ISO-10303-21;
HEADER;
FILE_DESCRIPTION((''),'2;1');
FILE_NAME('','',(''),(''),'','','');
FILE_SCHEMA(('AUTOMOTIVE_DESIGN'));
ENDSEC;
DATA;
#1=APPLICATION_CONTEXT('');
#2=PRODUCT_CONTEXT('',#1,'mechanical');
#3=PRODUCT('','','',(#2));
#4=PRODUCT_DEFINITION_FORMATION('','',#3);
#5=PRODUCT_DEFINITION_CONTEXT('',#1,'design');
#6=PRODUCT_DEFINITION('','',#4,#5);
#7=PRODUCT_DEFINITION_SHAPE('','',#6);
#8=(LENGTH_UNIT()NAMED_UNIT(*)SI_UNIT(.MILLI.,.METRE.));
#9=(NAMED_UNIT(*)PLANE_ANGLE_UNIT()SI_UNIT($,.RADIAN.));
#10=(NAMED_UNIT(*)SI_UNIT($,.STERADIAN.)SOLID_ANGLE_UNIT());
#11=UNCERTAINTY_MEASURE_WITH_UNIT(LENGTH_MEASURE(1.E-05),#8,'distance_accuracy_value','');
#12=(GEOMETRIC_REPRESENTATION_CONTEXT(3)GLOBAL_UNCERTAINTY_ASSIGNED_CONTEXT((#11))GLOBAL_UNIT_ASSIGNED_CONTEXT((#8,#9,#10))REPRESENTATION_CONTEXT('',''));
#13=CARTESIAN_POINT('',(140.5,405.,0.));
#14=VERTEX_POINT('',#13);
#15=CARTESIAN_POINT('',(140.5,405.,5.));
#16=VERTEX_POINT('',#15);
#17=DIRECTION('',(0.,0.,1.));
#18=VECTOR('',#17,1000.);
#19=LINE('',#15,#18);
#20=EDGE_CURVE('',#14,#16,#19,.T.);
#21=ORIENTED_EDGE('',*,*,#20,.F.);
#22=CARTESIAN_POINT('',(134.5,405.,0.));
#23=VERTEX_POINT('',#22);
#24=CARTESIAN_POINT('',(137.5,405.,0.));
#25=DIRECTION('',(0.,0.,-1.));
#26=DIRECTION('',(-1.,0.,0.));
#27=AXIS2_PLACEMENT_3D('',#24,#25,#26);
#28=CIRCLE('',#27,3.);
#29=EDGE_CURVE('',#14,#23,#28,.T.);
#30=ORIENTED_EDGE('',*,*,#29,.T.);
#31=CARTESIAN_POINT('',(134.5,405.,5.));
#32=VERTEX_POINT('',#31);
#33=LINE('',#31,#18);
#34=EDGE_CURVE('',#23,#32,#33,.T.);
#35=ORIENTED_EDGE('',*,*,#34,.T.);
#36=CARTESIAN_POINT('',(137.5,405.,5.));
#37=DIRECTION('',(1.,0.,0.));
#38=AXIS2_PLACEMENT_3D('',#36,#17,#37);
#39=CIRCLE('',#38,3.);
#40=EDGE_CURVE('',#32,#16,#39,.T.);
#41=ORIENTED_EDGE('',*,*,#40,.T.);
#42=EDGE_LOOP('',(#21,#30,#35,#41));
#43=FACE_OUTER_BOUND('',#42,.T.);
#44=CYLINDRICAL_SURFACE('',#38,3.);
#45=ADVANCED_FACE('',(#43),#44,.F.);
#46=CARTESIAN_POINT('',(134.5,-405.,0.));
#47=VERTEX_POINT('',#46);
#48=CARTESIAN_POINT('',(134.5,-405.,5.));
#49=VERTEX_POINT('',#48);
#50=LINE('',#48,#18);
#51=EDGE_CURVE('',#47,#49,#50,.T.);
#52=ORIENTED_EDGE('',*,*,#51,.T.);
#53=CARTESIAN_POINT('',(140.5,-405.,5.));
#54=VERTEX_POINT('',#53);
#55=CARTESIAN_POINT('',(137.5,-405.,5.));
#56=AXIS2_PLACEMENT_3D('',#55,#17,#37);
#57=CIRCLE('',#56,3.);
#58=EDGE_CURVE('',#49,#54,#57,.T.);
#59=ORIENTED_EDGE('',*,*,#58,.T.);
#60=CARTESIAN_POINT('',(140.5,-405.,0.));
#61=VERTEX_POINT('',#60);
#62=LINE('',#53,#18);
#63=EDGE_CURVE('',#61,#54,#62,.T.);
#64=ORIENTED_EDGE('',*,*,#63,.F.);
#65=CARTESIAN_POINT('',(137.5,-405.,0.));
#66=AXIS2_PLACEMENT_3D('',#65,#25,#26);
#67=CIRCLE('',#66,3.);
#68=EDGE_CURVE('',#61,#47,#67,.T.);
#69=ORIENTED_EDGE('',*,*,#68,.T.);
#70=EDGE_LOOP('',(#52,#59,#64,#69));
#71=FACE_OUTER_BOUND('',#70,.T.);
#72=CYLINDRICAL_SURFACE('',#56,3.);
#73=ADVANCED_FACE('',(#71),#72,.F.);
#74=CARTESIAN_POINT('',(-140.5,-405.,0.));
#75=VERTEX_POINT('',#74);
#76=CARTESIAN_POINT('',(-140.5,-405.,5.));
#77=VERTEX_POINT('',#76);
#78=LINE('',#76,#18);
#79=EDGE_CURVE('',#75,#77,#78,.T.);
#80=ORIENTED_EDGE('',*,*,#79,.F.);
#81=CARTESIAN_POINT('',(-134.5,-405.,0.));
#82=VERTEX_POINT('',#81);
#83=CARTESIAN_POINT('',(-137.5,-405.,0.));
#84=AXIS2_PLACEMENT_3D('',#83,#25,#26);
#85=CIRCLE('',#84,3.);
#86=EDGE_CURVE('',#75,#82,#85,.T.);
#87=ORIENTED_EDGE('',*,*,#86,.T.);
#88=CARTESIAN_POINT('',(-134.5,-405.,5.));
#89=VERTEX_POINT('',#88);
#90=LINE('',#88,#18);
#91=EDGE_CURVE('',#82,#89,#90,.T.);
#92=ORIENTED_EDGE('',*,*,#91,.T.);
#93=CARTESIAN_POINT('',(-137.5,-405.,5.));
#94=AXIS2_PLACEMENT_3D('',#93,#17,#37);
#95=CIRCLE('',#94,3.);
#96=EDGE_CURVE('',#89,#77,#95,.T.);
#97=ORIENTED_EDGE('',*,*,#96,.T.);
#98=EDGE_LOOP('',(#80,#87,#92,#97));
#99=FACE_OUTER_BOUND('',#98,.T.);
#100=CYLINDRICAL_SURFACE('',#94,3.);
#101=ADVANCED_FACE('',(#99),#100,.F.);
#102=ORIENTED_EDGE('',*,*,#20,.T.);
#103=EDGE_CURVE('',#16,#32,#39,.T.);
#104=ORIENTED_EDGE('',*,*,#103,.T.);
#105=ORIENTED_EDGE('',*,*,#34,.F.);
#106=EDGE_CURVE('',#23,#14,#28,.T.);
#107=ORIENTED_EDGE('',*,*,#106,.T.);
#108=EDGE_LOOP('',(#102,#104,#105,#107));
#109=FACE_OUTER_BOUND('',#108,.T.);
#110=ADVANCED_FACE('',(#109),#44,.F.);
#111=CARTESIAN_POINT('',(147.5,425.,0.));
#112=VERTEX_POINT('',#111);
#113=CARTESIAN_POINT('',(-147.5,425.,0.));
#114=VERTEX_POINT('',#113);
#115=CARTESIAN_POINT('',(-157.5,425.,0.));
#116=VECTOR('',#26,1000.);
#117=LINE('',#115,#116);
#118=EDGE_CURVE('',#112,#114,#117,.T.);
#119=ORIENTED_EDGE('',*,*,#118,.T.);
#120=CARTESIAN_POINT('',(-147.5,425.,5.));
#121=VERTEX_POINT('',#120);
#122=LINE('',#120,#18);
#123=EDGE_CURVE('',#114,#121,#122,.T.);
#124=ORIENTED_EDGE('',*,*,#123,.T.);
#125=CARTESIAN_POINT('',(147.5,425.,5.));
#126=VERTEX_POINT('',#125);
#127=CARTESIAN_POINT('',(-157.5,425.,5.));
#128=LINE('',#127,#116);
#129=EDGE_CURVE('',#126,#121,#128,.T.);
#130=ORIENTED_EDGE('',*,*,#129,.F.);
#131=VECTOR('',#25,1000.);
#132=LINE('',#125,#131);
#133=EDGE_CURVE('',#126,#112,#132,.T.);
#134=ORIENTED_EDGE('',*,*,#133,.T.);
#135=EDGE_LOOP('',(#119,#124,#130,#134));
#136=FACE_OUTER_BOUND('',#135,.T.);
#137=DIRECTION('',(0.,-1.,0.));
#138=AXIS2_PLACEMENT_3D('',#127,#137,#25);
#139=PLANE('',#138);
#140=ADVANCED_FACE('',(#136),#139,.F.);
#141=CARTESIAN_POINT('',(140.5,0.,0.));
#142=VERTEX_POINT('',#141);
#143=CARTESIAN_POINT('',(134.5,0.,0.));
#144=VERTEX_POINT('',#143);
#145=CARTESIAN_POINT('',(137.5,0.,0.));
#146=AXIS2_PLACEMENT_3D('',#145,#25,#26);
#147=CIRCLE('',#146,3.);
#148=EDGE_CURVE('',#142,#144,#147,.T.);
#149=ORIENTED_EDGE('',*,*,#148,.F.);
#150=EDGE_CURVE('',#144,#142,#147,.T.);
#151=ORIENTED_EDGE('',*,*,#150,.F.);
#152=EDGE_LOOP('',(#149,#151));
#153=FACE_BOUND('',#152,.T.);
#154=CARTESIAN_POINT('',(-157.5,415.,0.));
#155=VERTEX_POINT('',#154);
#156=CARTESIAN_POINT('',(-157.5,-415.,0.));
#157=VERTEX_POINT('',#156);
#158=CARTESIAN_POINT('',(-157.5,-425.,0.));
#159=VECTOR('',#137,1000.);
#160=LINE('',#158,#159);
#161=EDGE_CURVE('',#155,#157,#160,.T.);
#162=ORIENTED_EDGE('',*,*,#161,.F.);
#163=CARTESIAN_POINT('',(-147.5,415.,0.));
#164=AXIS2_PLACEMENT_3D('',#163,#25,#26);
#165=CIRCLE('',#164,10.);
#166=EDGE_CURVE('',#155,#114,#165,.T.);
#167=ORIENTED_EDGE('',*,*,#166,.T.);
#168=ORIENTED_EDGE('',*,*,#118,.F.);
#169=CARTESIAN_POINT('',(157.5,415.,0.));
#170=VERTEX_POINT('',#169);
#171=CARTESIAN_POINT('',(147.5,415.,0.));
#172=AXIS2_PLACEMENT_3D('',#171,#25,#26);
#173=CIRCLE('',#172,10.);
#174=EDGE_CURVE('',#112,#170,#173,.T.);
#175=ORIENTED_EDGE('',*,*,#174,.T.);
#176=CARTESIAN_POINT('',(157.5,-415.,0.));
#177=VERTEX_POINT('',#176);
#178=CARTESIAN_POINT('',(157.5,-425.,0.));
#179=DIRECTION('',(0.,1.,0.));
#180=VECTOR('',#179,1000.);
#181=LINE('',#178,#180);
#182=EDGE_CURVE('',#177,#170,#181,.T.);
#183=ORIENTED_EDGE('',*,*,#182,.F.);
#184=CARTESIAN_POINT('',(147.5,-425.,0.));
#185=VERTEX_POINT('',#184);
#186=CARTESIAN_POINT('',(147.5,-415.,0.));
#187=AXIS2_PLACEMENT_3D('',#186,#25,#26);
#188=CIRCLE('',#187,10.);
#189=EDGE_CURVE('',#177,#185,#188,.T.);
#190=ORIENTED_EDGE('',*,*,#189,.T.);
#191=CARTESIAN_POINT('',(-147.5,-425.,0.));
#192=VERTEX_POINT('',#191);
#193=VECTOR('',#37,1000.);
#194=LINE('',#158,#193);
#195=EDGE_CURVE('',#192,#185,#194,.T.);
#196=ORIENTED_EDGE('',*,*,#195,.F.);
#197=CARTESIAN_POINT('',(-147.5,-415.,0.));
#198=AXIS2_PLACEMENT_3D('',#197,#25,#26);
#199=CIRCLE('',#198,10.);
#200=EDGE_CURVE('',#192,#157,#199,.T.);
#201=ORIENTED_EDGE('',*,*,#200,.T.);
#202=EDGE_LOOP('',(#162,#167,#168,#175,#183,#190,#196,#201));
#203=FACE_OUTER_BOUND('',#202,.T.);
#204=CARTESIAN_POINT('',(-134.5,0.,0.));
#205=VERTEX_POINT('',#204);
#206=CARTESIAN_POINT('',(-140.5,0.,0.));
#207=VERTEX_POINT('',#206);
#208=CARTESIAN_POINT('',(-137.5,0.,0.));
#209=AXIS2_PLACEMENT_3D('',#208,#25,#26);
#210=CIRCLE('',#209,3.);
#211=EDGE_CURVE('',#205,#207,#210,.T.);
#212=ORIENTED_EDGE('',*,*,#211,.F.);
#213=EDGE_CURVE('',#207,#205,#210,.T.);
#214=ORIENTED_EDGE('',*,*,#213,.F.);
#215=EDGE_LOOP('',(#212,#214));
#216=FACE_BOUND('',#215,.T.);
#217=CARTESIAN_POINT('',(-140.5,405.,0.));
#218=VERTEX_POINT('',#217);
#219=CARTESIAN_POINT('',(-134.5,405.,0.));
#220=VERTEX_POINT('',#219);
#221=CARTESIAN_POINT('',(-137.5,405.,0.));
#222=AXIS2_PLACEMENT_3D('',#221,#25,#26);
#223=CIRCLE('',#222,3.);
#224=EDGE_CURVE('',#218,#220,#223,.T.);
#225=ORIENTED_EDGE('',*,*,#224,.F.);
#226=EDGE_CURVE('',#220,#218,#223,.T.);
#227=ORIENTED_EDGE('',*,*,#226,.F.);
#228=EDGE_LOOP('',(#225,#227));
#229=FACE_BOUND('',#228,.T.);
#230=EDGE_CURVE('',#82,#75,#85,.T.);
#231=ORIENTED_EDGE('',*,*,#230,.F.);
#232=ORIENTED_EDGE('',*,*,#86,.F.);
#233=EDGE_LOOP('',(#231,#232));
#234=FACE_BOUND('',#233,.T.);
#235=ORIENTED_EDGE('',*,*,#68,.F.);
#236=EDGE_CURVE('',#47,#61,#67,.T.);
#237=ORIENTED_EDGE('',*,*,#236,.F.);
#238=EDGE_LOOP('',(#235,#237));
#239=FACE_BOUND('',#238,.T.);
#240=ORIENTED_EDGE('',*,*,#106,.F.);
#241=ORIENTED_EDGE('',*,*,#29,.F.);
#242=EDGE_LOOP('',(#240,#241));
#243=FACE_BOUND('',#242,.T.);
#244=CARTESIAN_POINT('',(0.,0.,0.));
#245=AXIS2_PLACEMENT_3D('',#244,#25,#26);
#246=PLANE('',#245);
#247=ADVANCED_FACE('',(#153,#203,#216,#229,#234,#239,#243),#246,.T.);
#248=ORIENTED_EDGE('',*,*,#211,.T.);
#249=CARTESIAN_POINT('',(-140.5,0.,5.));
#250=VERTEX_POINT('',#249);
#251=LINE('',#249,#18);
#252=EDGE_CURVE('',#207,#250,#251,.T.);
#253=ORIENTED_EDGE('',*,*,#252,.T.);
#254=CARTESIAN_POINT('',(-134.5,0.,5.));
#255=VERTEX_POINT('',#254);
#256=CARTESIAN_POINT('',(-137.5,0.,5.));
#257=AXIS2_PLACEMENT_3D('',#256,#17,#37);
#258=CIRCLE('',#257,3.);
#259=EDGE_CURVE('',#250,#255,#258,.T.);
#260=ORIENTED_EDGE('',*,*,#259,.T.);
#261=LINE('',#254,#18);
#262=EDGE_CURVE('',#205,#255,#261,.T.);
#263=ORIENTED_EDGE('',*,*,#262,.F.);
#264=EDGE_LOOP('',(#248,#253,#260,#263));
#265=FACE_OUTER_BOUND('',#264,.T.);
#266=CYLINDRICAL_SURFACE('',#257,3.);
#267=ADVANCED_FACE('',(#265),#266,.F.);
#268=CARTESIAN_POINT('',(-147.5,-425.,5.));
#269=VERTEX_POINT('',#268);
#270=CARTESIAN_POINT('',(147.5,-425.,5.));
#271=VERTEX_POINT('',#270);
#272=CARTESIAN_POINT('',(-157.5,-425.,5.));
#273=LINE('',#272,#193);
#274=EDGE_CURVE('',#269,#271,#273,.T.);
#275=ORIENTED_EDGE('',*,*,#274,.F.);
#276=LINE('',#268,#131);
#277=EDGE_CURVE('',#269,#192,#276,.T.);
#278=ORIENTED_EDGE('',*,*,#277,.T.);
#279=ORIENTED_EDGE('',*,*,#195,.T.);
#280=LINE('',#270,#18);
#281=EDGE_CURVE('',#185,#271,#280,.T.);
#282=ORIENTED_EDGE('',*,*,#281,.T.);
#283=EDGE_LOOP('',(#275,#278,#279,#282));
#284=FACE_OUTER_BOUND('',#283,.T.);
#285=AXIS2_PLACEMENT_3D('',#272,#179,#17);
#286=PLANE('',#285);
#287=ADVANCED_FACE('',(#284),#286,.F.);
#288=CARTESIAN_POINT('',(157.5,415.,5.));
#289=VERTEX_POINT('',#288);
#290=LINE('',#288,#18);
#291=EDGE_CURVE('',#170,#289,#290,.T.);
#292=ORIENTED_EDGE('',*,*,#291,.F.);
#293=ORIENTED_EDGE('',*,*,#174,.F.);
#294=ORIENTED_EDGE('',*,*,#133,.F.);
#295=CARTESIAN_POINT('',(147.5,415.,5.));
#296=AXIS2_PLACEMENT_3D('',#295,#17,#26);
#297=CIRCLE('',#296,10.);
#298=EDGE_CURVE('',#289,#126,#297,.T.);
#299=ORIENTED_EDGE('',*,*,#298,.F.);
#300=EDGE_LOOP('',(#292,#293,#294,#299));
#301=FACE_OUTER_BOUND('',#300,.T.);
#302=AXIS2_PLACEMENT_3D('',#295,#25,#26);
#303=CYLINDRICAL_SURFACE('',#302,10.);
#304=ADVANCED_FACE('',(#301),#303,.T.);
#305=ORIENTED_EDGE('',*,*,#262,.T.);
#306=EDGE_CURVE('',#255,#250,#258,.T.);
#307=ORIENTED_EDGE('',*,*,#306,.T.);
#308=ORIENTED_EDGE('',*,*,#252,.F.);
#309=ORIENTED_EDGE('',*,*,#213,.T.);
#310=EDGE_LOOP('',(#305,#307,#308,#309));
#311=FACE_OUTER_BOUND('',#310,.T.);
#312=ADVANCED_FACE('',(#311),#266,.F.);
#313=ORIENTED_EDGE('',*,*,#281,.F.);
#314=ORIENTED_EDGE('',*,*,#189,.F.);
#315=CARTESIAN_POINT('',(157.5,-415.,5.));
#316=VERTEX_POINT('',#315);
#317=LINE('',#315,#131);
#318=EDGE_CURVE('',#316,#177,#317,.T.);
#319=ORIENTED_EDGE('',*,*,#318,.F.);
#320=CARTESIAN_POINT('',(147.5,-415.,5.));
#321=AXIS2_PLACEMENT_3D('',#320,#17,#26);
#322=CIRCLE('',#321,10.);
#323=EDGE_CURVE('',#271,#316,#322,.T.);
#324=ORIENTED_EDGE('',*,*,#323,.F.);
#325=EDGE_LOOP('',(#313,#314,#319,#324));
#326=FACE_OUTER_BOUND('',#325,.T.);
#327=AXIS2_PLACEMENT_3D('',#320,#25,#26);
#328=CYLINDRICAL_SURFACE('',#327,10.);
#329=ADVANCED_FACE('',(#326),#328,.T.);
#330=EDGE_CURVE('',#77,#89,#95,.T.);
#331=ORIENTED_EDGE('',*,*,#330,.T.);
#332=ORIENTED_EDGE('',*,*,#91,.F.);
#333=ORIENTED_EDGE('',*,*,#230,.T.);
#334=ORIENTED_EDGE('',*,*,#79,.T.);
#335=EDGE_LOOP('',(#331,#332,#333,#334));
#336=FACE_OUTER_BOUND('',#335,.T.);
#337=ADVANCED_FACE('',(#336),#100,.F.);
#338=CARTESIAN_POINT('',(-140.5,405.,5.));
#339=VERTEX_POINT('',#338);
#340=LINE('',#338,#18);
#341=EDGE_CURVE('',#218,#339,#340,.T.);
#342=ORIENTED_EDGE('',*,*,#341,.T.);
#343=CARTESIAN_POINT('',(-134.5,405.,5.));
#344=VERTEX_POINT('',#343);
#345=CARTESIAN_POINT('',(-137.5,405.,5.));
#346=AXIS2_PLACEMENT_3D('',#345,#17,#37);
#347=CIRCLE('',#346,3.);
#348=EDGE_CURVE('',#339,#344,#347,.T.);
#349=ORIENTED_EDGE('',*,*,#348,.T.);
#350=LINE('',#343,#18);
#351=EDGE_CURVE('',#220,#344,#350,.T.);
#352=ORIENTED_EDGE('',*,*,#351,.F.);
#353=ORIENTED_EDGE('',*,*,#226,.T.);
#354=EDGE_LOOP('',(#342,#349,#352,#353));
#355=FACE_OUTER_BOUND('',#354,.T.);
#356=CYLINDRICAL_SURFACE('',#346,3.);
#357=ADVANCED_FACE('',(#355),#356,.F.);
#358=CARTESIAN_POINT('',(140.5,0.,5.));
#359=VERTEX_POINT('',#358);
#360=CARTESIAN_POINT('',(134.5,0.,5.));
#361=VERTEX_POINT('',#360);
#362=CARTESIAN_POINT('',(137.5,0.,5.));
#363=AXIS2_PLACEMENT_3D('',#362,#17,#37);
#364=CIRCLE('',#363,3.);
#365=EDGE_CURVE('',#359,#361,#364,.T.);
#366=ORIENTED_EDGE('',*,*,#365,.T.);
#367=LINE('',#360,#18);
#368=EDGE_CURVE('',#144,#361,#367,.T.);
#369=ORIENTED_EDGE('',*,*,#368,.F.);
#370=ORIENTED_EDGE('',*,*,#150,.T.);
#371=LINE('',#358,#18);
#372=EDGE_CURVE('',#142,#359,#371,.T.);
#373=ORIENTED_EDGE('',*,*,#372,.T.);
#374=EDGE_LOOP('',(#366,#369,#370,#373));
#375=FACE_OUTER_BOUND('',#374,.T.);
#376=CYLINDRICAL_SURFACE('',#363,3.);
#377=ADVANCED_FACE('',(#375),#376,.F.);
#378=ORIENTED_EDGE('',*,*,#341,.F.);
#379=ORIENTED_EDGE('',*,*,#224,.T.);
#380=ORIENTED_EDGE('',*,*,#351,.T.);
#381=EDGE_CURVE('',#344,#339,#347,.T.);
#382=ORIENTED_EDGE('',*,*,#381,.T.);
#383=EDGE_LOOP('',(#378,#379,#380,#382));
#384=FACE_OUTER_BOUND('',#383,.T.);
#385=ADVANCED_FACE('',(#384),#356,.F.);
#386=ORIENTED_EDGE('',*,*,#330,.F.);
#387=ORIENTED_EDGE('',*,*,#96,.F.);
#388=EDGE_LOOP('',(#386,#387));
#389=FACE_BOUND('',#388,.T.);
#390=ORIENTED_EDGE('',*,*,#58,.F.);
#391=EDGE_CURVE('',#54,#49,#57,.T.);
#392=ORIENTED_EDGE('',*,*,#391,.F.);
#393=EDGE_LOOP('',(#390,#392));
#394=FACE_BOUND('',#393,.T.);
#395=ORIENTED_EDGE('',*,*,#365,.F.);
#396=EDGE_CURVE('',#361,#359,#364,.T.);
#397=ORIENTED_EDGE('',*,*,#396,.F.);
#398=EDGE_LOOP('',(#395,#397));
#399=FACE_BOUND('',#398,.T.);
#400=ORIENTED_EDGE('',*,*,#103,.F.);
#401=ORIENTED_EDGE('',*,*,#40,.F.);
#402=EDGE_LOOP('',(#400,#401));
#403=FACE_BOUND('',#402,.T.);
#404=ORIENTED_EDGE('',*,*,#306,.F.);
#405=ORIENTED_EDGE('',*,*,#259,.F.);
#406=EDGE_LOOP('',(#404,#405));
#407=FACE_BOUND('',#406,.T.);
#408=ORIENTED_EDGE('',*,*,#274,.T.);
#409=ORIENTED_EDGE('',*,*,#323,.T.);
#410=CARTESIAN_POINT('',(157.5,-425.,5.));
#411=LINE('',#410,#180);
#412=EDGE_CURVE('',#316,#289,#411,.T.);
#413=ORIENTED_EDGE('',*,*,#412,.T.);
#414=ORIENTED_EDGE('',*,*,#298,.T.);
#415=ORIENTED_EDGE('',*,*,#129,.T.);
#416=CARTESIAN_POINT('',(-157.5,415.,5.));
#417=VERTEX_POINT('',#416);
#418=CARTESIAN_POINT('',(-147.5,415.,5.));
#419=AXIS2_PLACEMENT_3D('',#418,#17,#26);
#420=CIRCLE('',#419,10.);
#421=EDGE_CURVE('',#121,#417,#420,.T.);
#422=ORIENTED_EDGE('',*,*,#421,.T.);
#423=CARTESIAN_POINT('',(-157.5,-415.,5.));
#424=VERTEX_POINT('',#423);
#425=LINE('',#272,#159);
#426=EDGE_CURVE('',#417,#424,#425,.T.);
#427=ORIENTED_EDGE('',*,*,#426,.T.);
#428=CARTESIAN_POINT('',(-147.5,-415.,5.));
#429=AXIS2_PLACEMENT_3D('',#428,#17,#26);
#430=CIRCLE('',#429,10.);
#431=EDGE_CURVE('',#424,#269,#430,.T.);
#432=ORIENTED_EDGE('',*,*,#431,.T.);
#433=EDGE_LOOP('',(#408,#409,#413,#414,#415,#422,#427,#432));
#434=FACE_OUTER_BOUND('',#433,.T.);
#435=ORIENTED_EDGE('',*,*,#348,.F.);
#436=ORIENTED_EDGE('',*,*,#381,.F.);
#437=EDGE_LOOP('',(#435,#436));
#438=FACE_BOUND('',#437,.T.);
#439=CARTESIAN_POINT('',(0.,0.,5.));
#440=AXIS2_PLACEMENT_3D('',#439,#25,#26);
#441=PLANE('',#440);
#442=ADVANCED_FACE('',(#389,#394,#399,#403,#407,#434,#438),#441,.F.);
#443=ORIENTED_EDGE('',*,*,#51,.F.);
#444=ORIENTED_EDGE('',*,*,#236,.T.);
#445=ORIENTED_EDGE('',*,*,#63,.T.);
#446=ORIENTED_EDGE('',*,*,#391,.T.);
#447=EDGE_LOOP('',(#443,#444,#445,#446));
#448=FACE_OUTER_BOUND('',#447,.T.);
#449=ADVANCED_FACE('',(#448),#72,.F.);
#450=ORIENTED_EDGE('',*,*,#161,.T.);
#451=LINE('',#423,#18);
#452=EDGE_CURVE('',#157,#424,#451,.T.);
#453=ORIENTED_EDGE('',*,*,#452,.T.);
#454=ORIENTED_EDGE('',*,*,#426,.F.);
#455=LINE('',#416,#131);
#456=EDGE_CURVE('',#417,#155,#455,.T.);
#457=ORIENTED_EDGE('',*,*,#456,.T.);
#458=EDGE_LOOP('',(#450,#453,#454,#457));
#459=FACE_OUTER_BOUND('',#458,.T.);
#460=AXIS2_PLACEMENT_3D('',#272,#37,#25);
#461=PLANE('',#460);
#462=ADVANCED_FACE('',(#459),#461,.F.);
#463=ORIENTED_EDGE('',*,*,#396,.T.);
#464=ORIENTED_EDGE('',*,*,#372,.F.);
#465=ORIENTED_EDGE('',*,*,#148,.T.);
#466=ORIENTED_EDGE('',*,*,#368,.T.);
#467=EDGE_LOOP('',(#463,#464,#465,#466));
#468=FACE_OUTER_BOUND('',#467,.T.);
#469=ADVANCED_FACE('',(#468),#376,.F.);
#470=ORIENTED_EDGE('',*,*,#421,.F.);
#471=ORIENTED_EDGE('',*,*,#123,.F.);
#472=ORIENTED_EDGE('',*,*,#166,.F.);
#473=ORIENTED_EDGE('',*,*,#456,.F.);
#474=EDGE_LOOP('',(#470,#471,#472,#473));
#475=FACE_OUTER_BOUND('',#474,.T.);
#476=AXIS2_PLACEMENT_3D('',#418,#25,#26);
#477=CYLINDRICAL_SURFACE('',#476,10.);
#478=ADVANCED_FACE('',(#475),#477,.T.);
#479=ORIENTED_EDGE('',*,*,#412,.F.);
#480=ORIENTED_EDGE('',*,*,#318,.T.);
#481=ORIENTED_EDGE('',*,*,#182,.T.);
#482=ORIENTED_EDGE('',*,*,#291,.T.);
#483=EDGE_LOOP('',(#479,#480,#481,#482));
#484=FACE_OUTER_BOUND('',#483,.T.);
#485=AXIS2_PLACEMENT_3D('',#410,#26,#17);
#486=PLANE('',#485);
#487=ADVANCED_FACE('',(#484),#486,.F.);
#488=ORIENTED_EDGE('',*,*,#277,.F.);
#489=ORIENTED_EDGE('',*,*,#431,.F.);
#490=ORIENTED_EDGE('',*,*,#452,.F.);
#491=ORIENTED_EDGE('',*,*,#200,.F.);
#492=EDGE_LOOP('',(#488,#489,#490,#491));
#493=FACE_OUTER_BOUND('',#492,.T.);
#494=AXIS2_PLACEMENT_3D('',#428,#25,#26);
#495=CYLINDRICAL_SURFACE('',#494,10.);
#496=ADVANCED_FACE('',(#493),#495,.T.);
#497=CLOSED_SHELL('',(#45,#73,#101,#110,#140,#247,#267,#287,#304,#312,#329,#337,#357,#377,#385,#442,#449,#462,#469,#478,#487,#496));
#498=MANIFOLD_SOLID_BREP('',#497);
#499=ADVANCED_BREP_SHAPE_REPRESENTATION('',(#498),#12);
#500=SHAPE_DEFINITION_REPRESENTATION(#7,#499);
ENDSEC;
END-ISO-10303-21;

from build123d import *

# Parameters (mm, degrees)
SKETCH_1_W                = 315
SKETCH_1_H                = 850
EXTRUDE_1_DEPTH           = 5
HOLE_WIZARD_6_0_6_1_D     = 6
HOLE_WIZARD_6_0_6_1_DEPTH = 27.75
HOLE_WIZARD_6_0_6_1_TIP   = 1.802581857
FILLET_1_R                = 10


with BuildPart() as part:
    # 草图1 → 凸台-拉伸1 (new body)
    with BuildSketch(Plane.XY):
        Rectangle(SKETCH_1_W, SKETCH_1_H)
    extrude(amount=EXTRUDE_1_DEPTH)

    # Ø6.0 (6) 直径孔1
    with Locations(Plane.XY.offset(5)):
        with Locations((-137.5, 405), (137.5, 405), (137.5, -405), (-137.5, -405), (-137.5, 0), (137.5, 0)):
            Hole(HOLE_WIZARD_6_0_6_1_D / 2, depth=HOLE_WIZARD_6_0_6_1_DEPTH)
            with Locations((0, 0, -(HOLE_WIZARD_6_0_6_1_DEPTH + HOLE_WIZARD_6_0_6_1_TIP / 2))):  # 118° drill point
                Cone(0, HOLE_WIZARD_6_0_6_1_D / 2, HOLE_WIZARD_6_0_6_1_TIP, mode=Mode.SUBTRACT)

    # 圆角1
    fillet_1_edges = [part.edges().sort_by_distance(p)[0] for p in [
        (157.5, -425, 2.5),
        (-157.5, -425, 2.5),
        (-157.5, 425, 2.5),
        (157.5, 425, 2.5),
    ]]
    fillet(fillet_1_edges, radius=FILLET_1_R)


solid = part.part
